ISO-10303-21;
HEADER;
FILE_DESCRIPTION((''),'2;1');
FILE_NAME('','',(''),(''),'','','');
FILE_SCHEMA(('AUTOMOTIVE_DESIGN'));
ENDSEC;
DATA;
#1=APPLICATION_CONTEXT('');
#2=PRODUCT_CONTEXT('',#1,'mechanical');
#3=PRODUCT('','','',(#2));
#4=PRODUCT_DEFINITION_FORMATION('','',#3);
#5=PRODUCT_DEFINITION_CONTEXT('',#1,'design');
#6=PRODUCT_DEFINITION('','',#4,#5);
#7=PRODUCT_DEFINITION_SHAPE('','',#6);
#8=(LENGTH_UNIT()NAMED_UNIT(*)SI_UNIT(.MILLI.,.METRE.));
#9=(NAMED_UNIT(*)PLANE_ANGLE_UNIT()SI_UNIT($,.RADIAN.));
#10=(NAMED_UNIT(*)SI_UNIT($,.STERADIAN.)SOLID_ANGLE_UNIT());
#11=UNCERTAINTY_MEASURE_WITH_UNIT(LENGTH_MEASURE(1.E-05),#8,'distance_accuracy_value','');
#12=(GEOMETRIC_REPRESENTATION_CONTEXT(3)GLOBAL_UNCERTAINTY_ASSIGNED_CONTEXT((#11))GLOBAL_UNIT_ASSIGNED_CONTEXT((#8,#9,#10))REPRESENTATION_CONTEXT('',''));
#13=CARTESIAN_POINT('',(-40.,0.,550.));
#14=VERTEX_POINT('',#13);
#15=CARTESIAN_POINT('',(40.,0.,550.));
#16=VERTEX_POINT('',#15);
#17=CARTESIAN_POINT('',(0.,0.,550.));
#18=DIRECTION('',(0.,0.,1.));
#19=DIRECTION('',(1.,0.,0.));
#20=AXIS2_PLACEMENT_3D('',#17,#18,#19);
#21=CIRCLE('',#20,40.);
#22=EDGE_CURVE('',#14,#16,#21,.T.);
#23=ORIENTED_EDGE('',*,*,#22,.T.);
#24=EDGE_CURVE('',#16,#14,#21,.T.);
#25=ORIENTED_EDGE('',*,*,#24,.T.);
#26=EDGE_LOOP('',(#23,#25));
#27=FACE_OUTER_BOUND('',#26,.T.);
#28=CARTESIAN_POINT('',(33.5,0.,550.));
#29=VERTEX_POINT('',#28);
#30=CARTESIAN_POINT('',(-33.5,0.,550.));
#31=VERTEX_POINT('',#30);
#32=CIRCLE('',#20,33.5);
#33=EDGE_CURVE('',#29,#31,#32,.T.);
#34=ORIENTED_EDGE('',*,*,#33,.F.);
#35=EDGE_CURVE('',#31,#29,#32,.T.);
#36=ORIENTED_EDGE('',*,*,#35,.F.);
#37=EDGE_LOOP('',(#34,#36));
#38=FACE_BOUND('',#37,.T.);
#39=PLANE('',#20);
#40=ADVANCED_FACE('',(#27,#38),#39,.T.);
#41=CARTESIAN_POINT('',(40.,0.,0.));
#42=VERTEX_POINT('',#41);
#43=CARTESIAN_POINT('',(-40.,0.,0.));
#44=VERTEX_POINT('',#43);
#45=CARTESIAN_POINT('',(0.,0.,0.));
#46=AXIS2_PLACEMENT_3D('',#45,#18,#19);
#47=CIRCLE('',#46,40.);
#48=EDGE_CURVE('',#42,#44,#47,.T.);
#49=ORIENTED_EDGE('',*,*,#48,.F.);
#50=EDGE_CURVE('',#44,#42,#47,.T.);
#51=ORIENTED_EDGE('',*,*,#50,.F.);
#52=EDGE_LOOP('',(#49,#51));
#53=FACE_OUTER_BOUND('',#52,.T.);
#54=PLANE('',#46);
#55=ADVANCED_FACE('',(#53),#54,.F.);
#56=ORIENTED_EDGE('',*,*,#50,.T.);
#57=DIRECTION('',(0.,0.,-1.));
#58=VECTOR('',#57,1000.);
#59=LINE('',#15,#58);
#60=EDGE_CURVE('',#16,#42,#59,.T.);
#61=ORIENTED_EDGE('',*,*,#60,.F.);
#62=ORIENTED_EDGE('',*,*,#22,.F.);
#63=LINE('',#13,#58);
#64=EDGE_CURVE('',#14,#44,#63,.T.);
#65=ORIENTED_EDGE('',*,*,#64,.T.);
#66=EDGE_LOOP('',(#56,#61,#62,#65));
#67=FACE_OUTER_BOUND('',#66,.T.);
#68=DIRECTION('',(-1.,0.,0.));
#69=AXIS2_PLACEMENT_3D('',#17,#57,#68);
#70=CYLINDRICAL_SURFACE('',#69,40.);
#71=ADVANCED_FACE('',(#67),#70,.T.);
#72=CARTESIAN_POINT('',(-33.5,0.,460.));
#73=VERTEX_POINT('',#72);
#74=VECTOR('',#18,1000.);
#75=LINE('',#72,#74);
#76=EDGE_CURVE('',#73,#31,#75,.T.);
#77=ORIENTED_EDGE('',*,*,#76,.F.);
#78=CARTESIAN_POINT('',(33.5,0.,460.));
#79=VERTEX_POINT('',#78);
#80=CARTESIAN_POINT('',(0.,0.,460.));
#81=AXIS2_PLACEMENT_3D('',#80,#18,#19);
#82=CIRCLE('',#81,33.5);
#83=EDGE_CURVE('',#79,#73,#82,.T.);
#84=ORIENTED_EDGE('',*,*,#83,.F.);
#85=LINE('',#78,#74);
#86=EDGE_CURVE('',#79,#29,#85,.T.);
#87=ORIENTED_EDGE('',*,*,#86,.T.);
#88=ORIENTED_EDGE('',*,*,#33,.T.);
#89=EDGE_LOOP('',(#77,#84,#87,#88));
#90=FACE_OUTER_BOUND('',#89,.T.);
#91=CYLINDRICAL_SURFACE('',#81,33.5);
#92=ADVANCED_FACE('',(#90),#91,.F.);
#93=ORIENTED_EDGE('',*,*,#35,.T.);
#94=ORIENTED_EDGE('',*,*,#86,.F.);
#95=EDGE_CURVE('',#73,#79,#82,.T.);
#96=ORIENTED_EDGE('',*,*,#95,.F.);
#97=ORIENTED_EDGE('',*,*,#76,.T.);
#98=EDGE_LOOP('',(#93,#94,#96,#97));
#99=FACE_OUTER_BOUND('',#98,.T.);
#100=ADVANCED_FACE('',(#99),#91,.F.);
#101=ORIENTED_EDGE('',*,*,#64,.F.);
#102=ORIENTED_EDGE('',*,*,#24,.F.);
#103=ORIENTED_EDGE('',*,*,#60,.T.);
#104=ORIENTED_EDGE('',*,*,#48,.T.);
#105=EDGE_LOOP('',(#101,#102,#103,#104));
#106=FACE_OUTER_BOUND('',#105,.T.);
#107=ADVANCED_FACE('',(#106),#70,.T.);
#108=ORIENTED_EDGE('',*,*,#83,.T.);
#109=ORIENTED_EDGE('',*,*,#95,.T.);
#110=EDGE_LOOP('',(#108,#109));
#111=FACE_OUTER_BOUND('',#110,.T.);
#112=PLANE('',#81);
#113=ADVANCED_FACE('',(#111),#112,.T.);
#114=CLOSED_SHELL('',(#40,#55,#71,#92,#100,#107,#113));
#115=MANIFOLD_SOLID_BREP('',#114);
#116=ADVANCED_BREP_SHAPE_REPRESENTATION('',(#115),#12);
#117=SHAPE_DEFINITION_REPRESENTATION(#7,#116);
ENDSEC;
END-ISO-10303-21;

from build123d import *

# Parameters (mm, degrees)
SKETCH1_R           = 40
BOSS_EXTRUDE1_DEPTH = 550
SKETCH2_R           = 33.5
CUT_EXTRUDE1_DEPTH  = 90


with BuildPart() as part:
    # Sketch1 → Boss-Extrude1 (new body)
    with BuildSketch(Plane.XY):
        Circle(SKETCH1_R)
    extrude(amount=BOSS_EXTRUDE1_DEPTH)

    # Sketch2 → Cut-Extrude1 (cut)
    with BuildSketch(Plane.XY.offset(550)):
        Circle(SKETCH2_R)
    extrude(amount=-CUT_EXTRUDE1_DEPTH, mode=Mode.SUBTRACT)


solid = part.part
